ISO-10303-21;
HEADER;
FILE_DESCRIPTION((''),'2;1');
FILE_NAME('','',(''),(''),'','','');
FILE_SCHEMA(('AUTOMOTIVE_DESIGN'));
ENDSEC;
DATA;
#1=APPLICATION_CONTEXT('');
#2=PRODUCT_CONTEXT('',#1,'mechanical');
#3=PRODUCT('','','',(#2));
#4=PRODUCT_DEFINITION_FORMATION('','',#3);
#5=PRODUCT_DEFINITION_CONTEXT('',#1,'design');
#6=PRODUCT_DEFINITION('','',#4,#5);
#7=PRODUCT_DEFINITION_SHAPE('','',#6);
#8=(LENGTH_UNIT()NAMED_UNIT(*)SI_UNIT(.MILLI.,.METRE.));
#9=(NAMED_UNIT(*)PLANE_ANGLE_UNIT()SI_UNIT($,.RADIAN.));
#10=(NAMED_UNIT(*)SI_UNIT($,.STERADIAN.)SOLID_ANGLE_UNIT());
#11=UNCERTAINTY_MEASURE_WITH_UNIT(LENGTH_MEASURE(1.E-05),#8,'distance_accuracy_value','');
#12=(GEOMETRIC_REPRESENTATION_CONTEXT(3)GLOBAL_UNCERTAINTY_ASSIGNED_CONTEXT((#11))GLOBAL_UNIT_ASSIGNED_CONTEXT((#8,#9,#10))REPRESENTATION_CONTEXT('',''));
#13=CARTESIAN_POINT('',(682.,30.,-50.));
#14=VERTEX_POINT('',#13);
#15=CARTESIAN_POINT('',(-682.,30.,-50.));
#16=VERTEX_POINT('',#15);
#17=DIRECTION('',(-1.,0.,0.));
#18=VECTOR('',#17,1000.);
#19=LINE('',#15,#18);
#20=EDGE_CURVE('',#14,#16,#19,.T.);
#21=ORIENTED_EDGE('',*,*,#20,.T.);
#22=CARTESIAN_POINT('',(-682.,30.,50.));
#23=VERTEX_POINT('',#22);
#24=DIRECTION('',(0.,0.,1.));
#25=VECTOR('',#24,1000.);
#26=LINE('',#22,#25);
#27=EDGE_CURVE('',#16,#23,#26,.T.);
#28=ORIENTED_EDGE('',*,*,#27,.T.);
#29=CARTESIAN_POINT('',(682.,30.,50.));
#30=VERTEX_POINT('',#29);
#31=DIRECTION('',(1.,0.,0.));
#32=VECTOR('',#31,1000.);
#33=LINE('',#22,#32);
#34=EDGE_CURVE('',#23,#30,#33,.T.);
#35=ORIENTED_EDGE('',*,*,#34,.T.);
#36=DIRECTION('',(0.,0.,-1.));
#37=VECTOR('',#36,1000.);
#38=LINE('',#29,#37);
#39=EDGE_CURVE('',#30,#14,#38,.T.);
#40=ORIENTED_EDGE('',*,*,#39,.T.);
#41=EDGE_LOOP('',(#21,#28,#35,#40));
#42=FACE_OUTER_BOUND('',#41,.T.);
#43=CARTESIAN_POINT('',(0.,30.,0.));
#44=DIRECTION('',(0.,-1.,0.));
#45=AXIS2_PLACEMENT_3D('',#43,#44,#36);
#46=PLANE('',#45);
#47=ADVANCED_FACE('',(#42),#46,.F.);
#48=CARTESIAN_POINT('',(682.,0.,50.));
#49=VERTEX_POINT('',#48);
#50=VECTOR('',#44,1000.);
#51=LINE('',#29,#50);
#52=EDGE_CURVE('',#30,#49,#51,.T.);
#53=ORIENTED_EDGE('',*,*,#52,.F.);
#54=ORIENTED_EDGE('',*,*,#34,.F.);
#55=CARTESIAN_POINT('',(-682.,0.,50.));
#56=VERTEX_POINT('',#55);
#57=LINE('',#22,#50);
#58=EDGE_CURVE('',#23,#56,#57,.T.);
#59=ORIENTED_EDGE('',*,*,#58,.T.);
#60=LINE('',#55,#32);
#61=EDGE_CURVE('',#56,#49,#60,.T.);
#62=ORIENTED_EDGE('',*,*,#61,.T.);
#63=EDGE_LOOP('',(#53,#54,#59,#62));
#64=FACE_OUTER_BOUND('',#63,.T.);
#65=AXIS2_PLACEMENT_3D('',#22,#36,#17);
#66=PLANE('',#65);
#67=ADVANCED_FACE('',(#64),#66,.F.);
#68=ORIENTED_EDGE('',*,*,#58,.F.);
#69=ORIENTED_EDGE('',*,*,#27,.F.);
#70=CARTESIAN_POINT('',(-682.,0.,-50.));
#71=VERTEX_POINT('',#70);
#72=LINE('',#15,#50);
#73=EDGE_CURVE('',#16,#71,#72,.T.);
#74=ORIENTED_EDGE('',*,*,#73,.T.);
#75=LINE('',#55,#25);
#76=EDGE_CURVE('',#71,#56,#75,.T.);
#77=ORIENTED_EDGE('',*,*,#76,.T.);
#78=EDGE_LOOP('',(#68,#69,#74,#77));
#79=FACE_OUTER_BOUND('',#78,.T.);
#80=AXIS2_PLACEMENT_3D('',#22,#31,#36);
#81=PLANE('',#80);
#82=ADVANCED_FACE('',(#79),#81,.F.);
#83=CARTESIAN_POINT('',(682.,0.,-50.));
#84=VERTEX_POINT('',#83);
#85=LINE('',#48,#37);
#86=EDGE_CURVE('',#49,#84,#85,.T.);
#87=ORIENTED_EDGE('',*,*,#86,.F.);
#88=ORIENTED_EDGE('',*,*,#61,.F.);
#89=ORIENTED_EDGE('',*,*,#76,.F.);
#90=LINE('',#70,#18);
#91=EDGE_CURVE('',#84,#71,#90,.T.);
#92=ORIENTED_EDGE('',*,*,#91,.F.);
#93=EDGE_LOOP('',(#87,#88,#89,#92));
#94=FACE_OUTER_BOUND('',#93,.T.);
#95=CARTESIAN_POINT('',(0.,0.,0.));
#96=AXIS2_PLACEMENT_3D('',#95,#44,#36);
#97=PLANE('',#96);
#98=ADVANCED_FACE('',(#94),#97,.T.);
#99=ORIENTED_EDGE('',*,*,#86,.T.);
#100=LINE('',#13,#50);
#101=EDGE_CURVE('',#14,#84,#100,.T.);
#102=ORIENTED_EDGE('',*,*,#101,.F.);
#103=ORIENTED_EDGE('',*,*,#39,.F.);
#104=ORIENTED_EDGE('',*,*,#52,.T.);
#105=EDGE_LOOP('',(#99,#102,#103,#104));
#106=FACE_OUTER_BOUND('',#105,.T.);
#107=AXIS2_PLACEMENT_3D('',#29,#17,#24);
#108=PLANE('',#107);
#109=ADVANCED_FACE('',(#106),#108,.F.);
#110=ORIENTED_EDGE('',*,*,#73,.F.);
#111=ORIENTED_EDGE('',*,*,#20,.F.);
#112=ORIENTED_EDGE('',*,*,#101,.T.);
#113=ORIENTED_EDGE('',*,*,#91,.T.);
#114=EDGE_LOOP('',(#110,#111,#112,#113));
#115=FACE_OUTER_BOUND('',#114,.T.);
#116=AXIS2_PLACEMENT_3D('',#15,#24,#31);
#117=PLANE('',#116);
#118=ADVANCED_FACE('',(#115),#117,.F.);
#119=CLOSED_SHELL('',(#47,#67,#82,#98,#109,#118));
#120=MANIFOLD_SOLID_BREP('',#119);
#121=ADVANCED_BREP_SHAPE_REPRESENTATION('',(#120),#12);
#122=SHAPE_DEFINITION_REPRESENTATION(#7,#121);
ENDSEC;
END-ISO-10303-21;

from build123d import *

# Parameters (mm, degrees)
SKETCH1_W           = 1364
SKETCH1_H           = 100
BOSS_EXTRUDE1_DEPTH = 30


with BuildPart() as part:
    # Sketch1 → Boss-Extrude1 (new body)
    with BuildSketch(Plane(origin=(0, 0, 0), x_dir=(1, 0, 0), z_dir=(0, 1, 0))):
        Rectangle(SKETCH1_W, SKETCH1_H)
    extrude(amount=BOSS_EXTRUDE1_DEPTH)


solid = part.part
